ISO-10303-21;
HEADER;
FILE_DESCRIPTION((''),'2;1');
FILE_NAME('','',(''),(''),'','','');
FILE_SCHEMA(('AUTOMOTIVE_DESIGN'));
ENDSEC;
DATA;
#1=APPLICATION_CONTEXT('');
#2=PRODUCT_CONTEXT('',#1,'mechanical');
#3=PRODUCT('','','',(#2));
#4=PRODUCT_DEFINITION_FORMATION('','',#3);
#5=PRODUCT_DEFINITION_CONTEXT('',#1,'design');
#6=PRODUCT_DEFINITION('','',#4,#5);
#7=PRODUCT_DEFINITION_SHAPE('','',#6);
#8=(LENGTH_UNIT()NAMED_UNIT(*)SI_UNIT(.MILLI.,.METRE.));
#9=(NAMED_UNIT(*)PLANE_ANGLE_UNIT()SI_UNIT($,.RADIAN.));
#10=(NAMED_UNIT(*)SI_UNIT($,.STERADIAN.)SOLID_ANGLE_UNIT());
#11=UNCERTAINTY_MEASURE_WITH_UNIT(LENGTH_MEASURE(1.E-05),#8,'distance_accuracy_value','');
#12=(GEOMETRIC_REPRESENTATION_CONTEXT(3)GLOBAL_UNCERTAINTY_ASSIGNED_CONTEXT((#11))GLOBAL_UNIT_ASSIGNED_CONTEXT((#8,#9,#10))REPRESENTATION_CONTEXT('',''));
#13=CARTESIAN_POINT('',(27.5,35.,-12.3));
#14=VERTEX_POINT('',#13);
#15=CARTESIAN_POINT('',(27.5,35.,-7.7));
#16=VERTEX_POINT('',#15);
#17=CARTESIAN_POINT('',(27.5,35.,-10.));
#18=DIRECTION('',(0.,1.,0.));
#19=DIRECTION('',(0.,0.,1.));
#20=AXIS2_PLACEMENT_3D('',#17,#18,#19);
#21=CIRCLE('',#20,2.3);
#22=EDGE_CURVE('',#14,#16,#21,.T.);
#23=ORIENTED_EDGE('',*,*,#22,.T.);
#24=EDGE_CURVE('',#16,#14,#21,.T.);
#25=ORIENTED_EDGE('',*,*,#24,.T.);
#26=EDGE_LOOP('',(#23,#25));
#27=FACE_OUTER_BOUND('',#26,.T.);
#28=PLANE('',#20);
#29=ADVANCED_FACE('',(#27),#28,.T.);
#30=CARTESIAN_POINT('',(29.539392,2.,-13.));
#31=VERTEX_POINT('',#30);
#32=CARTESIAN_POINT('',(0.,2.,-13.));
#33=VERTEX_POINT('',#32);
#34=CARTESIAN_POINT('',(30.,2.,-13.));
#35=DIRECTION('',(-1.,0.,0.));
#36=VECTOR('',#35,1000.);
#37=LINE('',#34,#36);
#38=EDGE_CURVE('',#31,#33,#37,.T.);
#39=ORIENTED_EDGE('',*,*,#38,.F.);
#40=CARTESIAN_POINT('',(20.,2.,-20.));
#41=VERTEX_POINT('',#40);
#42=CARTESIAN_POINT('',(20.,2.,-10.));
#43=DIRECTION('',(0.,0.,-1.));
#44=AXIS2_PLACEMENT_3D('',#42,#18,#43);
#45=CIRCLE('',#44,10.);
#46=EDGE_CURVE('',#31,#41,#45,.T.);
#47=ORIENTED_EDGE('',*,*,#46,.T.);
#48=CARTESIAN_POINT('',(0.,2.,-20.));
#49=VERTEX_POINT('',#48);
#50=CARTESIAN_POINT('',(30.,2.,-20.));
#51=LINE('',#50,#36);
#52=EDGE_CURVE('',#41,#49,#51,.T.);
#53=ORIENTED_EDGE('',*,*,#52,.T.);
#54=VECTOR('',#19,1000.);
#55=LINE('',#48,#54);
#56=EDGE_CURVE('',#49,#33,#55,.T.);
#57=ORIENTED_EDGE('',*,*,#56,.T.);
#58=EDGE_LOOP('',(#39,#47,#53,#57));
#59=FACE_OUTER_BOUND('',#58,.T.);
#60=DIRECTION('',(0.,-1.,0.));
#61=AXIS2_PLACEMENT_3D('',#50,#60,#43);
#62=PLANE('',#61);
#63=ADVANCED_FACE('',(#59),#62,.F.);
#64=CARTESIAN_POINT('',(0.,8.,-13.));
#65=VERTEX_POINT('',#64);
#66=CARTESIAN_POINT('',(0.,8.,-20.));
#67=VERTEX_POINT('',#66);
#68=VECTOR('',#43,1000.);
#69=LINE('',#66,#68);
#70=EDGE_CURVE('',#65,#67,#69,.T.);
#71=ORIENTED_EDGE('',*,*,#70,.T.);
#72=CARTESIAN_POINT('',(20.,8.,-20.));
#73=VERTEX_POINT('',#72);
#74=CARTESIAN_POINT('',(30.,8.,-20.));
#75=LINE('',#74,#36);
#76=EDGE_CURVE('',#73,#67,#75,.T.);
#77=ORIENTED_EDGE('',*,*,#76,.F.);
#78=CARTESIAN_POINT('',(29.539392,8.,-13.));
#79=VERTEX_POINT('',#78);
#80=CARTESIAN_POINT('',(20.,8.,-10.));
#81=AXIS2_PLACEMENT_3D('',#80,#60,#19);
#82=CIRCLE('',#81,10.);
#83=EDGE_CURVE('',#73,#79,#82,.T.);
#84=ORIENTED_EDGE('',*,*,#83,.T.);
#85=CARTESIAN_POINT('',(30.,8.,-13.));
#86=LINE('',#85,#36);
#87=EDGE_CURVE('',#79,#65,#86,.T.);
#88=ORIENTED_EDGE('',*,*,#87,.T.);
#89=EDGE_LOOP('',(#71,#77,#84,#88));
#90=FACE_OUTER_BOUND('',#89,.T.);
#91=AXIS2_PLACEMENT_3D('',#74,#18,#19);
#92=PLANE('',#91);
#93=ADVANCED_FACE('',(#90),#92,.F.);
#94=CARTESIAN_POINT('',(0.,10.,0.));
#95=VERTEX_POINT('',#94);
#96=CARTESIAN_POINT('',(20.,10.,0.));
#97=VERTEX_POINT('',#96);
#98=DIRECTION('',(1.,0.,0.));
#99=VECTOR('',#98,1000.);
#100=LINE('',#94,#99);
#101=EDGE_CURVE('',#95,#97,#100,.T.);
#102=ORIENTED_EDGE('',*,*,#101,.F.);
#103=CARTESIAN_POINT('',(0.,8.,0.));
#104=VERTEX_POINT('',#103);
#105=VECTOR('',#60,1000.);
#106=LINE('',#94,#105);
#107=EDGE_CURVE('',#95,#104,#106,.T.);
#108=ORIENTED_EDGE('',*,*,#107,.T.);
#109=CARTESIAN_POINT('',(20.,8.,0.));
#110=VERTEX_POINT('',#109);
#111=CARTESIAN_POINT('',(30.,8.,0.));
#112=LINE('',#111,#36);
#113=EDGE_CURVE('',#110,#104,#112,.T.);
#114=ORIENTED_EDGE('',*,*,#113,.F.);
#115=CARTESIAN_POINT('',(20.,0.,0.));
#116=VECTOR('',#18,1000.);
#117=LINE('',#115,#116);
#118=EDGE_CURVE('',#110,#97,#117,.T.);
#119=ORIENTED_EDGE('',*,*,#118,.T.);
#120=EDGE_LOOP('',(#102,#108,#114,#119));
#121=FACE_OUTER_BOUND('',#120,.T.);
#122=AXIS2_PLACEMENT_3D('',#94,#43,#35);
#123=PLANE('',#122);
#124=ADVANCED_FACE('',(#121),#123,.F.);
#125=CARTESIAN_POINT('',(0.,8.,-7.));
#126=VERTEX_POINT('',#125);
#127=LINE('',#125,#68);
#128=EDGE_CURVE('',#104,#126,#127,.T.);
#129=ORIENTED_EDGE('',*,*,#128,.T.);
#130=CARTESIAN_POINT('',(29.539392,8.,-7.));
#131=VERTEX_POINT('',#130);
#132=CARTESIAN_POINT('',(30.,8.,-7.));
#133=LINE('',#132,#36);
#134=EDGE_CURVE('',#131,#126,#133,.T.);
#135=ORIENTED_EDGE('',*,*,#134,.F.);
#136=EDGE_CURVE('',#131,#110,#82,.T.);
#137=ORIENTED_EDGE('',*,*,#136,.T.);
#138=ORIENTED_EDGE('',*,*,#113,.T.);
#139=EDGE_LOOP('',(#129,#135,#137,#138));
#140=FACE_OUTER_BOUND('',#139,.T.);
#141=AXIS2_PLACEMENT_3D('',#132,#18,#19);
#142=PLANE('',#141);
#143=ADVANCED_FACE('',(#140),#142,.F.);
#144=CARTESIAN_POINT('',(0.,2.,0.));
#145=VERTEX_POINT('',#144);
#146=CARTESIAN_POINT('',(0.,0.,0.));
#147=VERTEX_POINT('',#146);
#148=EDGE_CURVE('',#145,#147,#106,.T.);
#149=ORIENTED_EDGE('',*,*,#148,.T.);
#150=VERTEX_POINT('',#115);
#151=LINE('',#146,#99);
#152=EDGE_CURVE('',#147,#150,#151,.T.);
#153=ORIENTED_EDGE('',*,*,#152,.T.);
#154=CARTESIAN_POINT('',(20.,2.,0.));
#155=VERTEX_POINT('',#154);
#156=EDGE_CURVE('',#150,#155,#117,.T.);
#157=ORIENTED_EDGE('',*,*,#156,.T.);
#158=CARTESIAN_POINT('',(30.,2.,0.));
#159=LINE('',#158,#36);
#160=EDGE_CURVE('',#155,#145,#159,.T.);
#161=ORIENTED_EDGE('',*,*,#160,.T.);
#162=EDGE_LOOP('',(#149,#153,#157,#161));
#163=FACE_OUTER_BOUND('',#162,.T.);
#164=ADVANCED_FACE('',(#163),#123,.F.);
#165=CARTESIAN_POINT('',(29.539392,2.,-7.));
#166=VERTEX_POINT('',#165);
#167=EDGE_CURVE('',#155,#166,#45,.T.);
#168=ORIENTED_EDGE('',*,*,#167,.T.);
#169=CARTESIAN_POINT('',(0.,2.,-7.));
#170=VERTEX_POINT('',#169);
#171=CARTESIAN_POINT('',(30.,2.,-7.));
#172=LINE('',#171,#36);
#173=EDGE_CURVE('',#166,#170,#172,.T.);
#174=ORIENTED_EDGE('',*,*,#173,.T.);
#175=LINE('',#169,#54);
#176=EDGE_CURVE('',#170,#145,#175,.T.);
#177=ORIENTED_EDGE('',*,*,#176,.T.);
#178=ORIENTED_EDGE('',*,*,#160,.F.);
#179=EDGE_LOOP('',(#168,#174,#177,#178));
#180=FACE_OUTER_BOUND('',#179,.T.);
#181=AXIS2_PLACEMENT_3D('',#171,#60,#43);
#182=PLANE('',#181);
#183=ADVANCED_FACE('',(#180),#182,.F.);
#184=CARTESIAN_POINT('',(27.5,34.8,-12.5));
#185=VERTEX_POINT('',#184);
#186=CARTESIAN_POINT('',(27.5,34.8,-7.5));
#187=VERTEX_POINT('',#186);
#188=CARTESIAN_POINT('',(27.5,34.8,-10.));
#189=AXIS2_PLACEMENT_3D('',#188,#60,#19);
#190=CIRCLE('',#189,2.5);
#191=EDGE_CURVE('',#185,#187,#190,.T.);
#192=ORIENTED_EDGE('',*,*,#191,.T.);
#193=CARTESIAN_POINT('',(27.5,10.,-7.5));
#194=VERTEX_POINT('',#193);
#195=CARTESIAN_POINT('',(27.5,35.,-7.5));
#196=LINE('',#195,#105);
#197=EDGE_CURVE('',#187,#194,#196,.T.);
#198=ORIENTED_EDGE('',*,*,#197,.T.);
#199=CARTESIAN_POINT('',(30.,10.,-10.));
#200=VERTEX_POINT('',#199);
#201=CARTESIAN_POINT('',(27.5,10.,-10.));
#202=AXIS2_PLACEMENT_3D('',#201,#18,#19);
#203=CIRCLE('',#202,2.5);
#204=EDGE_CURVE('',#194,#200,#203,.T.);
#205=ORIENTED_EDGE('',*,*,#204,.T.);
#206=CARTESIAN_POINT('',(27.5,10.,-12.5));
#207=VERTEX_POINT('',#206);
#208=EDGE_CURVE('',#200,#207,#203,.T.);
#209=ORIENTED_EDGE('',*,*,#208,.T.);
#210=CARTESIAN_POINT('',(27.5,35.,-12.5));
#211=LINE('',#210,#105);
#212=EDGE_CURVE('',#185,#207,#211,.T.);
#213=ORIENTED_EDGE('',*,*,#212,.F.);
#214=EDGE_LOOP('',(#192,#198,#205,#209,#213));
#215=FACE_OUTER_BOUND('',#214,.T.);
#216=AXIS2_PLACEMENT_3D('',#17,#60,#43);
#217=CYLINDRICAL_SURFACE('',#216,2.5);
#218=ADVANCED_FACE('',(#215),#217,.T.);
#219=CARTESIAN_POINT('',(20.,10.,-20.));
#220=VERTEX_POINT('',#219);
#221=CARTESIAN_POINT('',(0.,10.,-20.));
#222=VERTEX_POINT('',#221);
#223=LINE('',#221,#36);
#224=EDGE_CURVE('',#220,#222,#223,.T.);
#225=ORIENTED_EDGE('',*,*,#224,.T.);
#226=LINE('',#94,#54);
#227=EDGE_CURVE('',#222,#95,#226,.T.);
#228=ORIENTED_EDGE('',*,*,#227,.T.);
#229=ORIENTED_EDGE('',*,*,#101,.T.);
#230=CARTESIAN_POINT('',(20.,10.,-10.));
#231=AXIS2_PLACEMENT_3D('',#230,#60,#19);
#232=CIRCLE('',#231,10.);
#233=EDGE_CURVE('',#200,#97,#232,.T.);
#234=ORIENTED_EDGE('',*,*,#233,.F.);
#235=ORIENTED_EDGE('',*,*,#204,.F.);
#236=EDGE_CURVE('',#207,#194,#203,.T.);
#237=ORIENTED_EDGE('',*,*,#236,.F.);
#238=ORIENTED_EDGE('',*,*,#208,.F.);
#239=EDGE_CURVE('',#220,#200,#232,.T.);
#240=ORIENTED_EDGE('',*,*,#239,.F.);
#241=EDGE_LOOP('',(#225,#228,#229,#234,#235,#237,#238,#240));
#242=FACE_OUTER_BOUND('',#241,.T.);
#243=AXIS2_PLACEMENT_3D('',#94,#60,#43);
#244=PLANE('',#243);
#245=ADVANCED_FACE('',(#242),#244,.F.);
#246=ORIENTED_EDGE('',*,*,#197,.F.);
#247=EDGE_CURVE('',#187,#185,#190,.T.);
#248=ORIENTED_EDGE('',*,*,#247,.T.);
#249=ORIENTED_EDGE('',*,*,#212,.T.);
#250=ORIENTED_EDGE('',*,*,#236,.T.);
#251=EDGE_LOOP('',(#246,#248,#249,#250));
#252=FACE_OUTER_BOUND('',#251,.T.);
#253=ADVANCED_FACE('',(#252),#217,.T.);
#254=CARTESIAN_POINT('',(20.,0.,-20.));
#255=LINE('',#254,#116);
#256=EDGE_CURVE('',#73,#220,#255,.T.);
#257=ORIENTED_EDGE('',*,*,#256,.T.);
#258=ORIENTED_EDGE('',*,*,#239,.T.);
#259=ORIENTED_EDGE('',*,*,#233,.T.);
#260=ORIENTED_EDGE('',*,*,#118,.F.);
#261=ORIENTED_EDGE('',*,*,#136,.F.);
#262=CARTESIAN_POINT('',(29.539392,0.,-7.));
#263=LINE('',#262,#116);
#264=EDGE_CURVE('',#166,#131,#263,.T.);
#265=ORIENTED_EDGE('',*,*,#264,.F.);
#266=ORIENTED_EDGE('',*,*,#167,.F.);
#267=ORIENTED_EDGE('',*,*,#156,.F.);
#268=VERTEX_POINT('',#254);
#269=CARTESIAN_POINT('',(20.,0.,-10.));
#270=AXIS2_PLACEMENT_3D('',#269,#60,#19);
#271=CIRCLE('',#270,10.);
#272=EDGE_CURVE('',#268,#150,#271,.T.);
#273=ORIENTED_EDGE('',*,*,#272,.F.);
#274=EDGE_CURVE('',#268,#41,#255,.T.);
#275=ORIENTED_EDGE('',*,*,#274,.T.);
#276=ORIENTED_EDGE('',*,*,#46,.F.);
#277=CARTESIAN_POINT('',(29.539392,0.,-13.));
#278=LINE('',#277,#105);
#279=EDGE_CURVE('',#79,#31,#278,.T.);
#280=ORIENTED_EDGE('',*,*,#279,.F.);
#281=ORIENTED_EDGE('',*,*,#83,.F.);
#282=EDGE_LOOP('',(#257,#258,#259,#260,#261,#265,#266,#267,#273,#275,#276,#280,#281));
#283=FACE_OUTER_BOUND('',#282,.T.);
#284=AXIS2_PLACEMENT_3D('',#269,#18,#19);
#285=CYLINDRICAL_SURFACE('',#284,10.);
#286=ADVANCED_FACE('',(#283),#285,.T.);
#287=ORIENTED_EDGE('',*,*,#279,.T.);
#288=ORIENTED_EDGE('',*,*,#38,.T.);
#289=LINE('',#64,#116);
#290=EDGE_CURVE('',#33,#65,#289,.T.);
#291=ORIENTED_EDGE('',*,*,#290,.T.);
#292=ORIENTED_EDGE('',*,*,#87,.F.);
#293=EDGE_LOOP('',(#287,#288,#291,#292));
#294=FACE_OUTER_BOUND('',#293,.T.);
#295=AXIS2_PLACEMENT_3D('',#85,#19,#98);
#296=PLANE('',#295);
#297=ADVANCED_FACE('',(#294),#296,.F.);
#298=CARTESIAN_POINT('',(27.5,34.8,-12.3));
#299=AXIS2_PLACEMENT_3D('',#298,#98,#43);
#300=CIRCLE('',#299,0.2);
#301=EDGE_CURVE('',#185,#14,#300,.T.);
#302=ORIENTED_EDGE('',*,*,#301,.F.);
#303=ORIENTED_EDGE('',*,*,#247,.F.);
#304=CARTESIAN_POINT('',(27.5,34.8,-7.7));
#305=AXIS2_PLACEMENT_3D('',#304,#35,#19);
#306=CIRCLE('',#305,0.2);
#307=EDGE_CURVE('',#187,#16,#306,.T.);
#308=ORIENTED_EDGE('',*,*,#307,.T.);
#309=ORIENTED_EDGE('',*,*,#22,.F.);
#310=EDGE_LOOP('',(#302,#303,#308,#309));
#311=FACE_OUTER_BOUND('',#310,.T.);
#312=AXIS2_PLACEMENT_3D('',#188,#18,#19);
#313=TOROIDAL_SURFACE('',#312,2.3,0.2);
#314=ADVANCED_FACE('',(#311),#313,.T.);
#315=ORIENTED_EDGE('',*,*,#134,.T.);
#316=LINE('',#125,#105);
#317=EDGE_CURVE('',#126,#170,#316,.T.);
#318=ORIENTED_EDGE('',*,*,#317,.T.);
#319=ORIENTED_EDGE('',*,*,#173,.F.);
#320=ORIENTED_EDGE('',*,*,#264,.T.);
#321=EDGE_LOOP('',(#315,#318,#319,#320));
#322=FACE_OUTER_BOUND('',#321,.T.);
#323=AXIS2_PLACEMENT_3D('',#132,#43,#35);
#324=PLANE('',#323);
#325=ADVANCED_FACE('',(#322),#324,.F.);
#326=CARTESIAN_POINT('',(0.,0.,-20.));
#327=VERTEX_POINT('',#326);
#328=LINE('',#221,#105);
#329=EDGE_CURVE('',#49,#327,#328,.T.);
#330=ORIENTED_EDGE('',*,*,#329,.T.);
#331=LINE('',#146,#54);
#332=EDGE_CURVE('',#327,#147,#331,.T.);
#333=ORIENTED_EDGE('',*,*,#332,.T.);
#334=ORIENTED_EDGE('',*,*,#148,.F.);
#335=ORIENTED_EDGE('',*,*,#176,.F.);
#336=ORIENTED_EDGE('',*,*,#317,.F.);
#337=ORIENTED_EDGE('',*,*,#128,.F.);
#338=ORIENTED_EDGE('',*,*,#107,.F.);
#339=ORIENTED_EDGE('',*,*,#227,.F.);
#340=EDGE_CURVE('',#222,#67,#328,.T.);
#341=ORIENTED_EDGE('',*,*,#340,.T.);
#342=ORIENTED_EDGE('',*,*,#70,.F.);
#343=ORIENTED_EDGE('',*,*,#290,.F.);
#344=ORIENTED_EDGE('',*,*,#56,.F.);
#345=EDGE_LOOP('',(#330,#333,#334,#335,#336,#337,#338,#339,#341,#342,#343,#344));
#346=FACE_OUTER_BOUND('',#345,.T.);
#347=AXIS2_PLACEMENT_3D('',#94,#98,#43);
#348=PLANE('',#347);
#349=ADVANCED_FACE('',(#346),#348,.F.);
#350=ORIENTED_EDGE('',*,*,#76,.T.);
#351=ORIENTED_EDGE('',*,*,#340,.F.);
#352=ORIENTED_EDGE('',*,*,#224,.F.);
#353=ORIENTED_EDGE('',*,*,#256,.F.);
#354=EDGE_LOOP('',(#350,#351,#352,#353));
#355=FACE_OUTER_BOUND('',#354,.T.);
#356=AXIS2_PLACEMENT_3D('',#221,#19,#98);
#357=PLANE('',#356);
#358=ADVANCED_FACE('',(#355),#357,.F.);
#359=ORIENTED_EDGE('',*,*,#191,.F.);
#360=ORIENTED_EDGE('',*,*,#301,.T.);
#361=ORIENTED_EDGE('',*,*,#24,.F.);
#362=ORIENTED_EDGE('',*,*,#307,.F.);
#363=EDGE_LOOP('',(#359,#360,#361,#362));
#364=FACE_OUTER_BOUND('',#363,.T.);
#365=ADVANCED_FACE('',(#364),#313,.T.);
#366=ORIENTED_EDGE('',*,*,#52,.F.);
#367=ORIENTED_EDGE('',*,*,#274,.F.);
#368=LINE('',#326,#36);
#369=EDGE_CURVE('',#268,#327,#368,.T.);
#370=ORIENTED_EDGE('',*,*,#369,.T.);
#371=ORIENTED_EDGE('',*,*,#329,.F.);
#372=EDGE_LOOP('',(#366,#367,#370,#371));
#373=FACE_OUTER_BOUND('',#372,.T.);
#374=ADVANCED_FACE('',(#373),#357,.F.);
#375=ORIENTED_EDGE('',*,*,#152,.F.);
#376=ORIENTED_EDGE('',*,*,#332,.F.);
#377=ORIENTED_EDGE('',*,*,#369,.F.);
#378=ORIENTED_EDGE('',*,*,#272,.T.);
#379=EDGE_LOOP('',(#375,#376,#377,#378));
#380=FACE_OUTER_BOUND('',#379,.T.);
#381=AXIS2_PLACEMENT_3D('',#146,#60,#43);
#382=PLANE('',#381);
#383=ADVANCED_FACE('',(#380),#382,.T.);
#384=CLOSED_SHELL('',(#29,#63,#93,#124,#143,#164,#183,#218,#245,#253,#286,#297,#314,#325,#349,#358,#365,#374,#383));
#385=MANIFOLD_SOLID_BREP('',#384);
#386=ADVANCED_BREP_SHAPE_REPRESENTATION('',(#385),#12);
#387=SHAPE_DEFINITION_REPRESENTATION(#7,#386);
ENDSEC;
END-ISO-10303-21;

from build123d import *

# Parameters (mm, degrees)
SKETCH1_W           = 30
SKETCH1_H           = 20
BOSS_EXTRUDE1_DEPTH = 10
SKETCH2_W           = 7
SKETCH2_H           = 6
CUT_EXTRUDE1_DEPTH  = 38.416573868
CUT_EXTRUDE2_DEPTH  = 38.416573868
SKETCH4_R           = 2.5
BOSS_EXTRUDE2_DEPTH = 25
FILLET1_R           = 0.2


with BuildPart() as part:
    # Sketch1 → Boss-Extrude1 (new body)
    with BuildSketch(Plane(origin=(0, 0, 0), x_dir=(1, 0, 0), z_dir=(0, 1, 0))):
        with Locations((15, 10)):
            Rectangle(SKETCH1_W, SKETCH1_H)
    extrude(amount=BOSS_EXTRUDE1_DEPTH)

    # Sketch2 → Cut-Extrude1 (cut, through all)
    with BuildSketch(Plane.ZY):
        with Locations((-16.5, 5)):
            Rectangle(SKETCH2_W, SKETCH2_H)
        with Locations((-3.5, 5)):
            Rectangle(SKETCH2_W, SKETCH2_H)
    extrude(amount=-CUT_EXTRUDE1_DEPTH, mode=Mode.SUBTRACT)

    # Sketch3 → Cut-Extrude2 (cut, through all)
    with BuildSketch(Plane(origin=(0, 10, 0), x_dir=(1, 0, 0), z_dir=(0, 1, 0))):
        with BuildLine():
            Line((30, 0), (30, 10))
            ThreePointArc((30, 10), (27.071067812, 2.928932188), (20, 0))
            Line((20, 0), (30, 0))
        make_face()
        with BuildLine():
            Line((30, 10), (30, 20))
            Line((30, 20), (20, 20))
            ThreePointArc((20, 20), (27.071067812, 17.071067812), (30, 10))
        make_face()
    extrude(amount=-CUT_EXTRUDE2_DEPTH, mode=Mode.SUBTRACT)

    # Sketch4 → Boss-Extrude2 (add)
    with BuildSketch(Plane(origin=(0, 10, 0), x_dir=(1, 0, 0), z_dir=(0, 1, 0))):
        with Locations(Location((27.5, 10, 0), (0, 0, 359.999408267))):
            Circle(SKETCH4_R)
    extrude(amount=BOSS_EXTRUDE2_DEPTH)

    # Fillet1
    fillet1_edges = [part.edges().sort_by_distance(p)[0] for p in [
        (25, 35, -10.000025819),
    ]]
    fillet(fillet1_edges, radius=FILLET1_R)


solid = part.part
